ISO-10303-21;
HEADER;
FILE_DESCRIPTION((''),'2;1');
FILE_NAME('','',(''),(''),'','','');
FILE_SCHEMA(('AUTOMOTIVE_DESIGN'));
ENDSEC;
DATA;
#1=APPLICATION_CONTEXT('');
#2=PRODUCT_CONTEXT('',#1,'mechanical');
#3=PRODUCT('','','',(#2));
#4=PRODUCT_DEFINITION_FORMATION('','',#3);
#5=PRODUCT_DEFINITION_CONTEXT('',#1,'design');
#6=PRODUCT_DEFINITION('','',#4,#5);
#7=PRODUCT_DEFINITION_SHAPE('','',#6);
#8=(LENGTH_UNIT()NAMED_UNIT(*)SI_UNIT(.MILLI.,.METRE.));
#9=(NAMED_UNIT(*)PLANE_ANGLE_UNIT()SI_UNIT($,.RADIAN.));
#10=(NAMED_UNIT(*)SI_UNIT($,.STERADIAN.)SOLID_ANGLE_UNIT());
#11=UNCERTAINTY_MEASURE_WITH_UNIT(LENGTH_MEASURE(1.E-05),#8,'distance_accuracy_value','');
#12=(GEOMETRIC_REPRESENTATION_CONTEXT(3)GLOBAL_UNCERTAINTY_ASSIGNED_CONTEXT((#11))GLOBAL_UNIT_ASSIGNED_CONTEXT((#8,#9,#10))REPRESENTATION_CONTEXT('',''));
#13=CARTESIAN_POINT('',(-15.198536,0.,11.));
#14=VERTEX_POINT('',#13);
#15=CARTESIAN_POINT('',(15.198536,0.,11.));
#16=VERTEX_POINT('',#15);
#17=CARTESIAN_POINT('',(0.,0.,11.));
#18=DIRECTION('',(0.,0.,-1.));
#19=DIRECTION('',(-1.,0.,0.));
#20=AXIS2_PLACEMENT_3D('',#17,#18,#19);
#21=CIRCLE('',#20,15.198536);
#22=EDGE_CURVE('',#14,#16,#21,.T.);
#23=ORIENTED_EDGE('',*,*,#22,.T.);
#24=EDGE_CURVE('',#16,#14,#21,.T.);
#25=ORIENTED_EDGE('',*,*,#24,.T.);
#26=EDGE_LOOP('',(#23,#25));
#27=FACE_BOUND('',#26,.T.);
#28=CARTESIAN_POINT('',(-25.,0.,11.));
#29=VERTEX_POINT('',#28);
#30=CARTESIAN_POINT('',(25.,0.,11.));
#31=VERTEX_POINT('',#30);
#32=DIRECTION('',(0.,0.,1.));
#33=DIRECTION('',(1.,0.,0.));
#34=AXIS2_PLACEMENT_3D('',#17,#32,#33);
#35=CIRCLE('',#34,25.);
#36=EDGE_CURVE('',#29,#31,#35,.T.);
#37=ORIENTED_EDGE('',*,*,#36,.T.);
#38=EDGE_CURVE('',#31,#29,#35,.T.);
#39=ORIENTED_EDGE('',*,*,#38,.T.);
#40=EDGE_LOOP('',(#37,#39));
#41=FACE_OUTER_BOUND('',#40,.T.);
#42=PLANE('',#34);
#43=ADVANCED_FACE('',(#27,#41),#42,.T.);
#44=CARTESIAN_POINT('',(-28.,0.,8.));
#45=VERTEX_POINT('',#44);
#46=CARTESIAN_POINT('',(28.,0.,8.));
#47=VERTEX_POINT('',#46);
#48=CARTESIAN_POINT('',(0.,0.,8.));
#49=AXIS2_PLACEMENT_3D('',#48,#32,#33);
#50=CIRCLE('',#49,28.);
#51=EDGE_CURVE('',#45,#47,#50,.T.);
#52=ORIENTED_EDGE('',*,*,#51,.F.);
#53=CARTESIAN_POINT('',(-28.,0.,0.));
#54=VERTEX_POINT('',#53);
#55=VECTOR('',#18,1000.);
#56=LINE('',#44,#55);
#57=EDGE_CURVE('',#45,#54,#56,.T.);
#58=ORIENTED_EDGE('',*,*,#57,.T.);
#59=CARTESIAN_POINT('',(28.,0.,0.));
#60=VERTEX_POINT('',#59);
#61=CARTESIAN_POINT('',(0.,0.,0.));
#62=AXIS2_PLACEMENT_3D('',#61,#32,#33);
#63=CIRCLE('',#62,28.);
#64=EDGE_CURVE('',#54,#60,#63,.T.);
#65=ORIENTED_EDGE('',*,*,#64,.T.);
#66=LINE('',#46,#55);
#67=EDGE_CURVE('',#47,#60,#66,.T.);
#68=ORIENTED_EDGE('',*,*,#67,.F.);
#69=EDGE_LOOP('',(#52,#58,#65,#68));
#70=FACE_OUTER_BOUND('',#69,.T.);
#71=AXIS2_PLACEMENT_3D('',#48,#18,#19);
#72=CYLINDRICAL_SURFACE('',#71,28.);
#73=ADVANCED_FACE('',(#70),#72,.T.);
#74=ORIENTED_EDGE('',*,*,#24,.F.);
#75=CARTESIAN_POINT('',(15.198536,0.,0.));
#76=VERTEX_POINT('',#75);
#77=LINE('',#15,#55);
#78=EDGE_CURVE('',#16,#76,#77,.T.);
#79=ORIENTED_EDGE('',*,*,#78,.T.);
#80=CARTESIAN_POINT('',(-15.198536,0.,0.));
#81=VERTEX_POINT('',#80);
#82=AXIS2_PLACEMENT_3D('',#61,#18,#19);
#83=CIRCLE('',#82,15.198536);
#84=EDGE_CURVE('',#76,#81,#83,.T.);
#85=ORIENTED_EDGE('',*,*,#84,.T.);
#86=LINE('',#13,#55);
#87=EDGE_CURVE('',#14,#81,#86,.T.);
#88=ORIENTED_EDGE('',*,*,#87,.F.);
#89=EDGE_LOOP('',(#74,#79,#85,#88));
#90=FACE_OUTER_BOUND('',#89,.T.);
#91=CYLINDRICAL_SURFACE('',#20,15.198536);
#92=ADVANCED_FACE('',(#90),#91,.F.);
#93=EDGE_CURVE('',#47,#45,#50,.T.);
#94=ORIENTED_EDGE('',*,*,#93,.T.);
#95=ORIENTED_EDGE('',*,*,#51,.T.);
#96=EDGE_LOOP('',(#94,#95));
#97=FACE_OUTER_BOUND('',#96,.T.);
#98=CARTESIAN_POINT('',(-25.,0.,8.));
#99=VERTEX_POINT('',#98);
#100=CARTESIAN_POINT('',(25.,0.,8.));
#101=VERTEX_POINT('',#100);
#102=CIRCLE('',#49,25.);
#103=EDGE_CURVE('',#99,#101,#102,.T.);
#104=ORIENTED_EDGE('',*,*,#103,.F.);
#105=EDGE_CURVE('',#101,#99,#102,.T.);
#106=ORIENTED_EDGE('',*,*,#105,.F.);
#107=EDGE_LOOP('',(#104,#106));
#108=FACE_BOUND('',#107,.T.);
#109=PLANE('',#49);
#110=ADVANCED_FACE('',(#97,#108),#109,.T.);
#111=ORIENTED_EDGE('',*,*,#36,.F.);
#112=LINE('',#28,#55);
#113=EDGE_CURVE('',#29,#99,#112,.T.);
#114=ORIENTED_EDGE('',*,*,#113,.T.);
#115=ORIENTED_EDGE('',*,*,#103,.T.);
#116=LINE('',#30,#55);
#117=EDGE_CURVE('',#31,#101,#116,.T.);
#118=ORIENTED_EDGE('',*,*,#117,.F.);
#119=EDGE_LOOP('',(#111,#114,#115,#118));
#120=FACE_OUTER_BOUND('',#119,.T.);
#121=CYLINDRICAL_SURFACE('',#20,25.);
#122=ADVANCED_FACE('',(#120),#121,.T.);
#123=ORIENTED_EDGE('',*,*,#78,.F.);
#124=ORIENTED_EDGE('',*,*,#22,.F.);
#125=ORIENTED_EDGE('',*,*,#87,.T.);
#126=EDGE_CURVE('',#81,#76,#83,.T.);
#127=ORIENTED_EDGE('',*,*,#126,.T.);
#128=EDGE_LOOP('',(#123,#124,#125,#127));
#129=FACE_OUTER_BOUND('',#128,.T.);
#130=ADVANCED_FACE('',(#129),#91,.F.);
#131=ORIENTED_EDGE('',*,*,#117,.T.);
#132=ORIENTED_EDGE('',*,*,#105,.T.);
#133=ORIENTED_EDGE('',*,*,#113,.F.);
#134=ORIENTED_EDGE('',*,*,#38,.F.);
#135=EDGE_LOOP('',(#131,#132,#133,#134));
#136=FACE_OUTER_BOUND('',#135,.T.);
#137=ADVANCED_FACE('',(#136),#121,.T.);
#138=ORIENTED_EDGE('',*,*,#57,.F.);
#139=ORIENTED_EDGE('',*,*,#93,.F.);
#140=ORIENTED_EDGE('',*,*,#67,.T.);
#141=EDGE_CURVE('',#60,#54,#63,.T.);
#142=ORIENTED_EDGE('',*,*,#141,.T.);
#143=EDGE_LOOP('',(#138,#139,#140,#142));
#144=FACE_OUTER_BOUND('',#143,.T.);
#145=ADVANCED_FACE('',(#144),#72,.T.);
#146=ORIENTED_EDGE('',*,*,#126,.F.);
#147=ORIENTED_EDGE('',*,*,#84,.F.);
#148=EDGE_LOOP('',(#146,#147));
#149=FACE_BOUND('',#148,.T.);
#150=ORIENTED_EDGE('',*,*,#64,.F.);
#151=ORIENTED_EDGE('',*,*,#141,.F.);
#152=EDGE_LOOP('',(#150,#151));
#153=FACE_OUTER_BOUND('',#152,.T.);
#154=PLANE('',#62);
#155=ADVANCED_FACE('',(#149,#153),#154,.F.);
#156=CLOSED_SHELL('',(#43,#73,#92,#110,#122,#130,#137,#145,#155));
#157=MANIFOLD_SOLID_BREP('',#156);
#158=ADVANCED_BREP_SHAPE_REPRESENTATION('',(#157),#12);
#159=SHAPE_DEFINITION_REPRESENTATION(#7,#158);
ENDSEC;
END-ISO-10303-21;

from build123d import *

# Parameters (mm, degrees)
SKETCH1_R           = 28
BOSS_EXTRUDE1_DEPTH = 8
SKETCH2_R           = 25
BOSS_EXTRUDE2_DEPTH = 3
SKETCH4_R           = 15.198536116
CUT_EXTRUDE1_DEPTH  = 42.097445176


with BuildPart() as part:
    # Sketch1 → Boss-Extrude1 (new body)
    with BuildSketch(Plane.XY):
        Circle(SKETCH1_R)
    extrude(amount=BOSS_EXTRUDE1_DEPTH)

    # Sketch2 → Boss-Extrude2 (add)
    with BuildSketch(Plane.XY.offset(8)):
        Circle(SKETCH2_R)
    extrude(amount=BOSS_EXTRUDE2_DEPTH)

    # Sketch4 → Cut-Extrude1 (cut, through all)
    with BuildSketch(Plane(origin=(0, 0, 0), x_dir=(-1, 0, 0), z_dir=(0, 0, -1))):
        Circle(SKETCH4_R)
    extrude(amount=-CUT_EXTRUDE1_DEPTH, mode=Mode.SUBTRACT)


solid = part.part
